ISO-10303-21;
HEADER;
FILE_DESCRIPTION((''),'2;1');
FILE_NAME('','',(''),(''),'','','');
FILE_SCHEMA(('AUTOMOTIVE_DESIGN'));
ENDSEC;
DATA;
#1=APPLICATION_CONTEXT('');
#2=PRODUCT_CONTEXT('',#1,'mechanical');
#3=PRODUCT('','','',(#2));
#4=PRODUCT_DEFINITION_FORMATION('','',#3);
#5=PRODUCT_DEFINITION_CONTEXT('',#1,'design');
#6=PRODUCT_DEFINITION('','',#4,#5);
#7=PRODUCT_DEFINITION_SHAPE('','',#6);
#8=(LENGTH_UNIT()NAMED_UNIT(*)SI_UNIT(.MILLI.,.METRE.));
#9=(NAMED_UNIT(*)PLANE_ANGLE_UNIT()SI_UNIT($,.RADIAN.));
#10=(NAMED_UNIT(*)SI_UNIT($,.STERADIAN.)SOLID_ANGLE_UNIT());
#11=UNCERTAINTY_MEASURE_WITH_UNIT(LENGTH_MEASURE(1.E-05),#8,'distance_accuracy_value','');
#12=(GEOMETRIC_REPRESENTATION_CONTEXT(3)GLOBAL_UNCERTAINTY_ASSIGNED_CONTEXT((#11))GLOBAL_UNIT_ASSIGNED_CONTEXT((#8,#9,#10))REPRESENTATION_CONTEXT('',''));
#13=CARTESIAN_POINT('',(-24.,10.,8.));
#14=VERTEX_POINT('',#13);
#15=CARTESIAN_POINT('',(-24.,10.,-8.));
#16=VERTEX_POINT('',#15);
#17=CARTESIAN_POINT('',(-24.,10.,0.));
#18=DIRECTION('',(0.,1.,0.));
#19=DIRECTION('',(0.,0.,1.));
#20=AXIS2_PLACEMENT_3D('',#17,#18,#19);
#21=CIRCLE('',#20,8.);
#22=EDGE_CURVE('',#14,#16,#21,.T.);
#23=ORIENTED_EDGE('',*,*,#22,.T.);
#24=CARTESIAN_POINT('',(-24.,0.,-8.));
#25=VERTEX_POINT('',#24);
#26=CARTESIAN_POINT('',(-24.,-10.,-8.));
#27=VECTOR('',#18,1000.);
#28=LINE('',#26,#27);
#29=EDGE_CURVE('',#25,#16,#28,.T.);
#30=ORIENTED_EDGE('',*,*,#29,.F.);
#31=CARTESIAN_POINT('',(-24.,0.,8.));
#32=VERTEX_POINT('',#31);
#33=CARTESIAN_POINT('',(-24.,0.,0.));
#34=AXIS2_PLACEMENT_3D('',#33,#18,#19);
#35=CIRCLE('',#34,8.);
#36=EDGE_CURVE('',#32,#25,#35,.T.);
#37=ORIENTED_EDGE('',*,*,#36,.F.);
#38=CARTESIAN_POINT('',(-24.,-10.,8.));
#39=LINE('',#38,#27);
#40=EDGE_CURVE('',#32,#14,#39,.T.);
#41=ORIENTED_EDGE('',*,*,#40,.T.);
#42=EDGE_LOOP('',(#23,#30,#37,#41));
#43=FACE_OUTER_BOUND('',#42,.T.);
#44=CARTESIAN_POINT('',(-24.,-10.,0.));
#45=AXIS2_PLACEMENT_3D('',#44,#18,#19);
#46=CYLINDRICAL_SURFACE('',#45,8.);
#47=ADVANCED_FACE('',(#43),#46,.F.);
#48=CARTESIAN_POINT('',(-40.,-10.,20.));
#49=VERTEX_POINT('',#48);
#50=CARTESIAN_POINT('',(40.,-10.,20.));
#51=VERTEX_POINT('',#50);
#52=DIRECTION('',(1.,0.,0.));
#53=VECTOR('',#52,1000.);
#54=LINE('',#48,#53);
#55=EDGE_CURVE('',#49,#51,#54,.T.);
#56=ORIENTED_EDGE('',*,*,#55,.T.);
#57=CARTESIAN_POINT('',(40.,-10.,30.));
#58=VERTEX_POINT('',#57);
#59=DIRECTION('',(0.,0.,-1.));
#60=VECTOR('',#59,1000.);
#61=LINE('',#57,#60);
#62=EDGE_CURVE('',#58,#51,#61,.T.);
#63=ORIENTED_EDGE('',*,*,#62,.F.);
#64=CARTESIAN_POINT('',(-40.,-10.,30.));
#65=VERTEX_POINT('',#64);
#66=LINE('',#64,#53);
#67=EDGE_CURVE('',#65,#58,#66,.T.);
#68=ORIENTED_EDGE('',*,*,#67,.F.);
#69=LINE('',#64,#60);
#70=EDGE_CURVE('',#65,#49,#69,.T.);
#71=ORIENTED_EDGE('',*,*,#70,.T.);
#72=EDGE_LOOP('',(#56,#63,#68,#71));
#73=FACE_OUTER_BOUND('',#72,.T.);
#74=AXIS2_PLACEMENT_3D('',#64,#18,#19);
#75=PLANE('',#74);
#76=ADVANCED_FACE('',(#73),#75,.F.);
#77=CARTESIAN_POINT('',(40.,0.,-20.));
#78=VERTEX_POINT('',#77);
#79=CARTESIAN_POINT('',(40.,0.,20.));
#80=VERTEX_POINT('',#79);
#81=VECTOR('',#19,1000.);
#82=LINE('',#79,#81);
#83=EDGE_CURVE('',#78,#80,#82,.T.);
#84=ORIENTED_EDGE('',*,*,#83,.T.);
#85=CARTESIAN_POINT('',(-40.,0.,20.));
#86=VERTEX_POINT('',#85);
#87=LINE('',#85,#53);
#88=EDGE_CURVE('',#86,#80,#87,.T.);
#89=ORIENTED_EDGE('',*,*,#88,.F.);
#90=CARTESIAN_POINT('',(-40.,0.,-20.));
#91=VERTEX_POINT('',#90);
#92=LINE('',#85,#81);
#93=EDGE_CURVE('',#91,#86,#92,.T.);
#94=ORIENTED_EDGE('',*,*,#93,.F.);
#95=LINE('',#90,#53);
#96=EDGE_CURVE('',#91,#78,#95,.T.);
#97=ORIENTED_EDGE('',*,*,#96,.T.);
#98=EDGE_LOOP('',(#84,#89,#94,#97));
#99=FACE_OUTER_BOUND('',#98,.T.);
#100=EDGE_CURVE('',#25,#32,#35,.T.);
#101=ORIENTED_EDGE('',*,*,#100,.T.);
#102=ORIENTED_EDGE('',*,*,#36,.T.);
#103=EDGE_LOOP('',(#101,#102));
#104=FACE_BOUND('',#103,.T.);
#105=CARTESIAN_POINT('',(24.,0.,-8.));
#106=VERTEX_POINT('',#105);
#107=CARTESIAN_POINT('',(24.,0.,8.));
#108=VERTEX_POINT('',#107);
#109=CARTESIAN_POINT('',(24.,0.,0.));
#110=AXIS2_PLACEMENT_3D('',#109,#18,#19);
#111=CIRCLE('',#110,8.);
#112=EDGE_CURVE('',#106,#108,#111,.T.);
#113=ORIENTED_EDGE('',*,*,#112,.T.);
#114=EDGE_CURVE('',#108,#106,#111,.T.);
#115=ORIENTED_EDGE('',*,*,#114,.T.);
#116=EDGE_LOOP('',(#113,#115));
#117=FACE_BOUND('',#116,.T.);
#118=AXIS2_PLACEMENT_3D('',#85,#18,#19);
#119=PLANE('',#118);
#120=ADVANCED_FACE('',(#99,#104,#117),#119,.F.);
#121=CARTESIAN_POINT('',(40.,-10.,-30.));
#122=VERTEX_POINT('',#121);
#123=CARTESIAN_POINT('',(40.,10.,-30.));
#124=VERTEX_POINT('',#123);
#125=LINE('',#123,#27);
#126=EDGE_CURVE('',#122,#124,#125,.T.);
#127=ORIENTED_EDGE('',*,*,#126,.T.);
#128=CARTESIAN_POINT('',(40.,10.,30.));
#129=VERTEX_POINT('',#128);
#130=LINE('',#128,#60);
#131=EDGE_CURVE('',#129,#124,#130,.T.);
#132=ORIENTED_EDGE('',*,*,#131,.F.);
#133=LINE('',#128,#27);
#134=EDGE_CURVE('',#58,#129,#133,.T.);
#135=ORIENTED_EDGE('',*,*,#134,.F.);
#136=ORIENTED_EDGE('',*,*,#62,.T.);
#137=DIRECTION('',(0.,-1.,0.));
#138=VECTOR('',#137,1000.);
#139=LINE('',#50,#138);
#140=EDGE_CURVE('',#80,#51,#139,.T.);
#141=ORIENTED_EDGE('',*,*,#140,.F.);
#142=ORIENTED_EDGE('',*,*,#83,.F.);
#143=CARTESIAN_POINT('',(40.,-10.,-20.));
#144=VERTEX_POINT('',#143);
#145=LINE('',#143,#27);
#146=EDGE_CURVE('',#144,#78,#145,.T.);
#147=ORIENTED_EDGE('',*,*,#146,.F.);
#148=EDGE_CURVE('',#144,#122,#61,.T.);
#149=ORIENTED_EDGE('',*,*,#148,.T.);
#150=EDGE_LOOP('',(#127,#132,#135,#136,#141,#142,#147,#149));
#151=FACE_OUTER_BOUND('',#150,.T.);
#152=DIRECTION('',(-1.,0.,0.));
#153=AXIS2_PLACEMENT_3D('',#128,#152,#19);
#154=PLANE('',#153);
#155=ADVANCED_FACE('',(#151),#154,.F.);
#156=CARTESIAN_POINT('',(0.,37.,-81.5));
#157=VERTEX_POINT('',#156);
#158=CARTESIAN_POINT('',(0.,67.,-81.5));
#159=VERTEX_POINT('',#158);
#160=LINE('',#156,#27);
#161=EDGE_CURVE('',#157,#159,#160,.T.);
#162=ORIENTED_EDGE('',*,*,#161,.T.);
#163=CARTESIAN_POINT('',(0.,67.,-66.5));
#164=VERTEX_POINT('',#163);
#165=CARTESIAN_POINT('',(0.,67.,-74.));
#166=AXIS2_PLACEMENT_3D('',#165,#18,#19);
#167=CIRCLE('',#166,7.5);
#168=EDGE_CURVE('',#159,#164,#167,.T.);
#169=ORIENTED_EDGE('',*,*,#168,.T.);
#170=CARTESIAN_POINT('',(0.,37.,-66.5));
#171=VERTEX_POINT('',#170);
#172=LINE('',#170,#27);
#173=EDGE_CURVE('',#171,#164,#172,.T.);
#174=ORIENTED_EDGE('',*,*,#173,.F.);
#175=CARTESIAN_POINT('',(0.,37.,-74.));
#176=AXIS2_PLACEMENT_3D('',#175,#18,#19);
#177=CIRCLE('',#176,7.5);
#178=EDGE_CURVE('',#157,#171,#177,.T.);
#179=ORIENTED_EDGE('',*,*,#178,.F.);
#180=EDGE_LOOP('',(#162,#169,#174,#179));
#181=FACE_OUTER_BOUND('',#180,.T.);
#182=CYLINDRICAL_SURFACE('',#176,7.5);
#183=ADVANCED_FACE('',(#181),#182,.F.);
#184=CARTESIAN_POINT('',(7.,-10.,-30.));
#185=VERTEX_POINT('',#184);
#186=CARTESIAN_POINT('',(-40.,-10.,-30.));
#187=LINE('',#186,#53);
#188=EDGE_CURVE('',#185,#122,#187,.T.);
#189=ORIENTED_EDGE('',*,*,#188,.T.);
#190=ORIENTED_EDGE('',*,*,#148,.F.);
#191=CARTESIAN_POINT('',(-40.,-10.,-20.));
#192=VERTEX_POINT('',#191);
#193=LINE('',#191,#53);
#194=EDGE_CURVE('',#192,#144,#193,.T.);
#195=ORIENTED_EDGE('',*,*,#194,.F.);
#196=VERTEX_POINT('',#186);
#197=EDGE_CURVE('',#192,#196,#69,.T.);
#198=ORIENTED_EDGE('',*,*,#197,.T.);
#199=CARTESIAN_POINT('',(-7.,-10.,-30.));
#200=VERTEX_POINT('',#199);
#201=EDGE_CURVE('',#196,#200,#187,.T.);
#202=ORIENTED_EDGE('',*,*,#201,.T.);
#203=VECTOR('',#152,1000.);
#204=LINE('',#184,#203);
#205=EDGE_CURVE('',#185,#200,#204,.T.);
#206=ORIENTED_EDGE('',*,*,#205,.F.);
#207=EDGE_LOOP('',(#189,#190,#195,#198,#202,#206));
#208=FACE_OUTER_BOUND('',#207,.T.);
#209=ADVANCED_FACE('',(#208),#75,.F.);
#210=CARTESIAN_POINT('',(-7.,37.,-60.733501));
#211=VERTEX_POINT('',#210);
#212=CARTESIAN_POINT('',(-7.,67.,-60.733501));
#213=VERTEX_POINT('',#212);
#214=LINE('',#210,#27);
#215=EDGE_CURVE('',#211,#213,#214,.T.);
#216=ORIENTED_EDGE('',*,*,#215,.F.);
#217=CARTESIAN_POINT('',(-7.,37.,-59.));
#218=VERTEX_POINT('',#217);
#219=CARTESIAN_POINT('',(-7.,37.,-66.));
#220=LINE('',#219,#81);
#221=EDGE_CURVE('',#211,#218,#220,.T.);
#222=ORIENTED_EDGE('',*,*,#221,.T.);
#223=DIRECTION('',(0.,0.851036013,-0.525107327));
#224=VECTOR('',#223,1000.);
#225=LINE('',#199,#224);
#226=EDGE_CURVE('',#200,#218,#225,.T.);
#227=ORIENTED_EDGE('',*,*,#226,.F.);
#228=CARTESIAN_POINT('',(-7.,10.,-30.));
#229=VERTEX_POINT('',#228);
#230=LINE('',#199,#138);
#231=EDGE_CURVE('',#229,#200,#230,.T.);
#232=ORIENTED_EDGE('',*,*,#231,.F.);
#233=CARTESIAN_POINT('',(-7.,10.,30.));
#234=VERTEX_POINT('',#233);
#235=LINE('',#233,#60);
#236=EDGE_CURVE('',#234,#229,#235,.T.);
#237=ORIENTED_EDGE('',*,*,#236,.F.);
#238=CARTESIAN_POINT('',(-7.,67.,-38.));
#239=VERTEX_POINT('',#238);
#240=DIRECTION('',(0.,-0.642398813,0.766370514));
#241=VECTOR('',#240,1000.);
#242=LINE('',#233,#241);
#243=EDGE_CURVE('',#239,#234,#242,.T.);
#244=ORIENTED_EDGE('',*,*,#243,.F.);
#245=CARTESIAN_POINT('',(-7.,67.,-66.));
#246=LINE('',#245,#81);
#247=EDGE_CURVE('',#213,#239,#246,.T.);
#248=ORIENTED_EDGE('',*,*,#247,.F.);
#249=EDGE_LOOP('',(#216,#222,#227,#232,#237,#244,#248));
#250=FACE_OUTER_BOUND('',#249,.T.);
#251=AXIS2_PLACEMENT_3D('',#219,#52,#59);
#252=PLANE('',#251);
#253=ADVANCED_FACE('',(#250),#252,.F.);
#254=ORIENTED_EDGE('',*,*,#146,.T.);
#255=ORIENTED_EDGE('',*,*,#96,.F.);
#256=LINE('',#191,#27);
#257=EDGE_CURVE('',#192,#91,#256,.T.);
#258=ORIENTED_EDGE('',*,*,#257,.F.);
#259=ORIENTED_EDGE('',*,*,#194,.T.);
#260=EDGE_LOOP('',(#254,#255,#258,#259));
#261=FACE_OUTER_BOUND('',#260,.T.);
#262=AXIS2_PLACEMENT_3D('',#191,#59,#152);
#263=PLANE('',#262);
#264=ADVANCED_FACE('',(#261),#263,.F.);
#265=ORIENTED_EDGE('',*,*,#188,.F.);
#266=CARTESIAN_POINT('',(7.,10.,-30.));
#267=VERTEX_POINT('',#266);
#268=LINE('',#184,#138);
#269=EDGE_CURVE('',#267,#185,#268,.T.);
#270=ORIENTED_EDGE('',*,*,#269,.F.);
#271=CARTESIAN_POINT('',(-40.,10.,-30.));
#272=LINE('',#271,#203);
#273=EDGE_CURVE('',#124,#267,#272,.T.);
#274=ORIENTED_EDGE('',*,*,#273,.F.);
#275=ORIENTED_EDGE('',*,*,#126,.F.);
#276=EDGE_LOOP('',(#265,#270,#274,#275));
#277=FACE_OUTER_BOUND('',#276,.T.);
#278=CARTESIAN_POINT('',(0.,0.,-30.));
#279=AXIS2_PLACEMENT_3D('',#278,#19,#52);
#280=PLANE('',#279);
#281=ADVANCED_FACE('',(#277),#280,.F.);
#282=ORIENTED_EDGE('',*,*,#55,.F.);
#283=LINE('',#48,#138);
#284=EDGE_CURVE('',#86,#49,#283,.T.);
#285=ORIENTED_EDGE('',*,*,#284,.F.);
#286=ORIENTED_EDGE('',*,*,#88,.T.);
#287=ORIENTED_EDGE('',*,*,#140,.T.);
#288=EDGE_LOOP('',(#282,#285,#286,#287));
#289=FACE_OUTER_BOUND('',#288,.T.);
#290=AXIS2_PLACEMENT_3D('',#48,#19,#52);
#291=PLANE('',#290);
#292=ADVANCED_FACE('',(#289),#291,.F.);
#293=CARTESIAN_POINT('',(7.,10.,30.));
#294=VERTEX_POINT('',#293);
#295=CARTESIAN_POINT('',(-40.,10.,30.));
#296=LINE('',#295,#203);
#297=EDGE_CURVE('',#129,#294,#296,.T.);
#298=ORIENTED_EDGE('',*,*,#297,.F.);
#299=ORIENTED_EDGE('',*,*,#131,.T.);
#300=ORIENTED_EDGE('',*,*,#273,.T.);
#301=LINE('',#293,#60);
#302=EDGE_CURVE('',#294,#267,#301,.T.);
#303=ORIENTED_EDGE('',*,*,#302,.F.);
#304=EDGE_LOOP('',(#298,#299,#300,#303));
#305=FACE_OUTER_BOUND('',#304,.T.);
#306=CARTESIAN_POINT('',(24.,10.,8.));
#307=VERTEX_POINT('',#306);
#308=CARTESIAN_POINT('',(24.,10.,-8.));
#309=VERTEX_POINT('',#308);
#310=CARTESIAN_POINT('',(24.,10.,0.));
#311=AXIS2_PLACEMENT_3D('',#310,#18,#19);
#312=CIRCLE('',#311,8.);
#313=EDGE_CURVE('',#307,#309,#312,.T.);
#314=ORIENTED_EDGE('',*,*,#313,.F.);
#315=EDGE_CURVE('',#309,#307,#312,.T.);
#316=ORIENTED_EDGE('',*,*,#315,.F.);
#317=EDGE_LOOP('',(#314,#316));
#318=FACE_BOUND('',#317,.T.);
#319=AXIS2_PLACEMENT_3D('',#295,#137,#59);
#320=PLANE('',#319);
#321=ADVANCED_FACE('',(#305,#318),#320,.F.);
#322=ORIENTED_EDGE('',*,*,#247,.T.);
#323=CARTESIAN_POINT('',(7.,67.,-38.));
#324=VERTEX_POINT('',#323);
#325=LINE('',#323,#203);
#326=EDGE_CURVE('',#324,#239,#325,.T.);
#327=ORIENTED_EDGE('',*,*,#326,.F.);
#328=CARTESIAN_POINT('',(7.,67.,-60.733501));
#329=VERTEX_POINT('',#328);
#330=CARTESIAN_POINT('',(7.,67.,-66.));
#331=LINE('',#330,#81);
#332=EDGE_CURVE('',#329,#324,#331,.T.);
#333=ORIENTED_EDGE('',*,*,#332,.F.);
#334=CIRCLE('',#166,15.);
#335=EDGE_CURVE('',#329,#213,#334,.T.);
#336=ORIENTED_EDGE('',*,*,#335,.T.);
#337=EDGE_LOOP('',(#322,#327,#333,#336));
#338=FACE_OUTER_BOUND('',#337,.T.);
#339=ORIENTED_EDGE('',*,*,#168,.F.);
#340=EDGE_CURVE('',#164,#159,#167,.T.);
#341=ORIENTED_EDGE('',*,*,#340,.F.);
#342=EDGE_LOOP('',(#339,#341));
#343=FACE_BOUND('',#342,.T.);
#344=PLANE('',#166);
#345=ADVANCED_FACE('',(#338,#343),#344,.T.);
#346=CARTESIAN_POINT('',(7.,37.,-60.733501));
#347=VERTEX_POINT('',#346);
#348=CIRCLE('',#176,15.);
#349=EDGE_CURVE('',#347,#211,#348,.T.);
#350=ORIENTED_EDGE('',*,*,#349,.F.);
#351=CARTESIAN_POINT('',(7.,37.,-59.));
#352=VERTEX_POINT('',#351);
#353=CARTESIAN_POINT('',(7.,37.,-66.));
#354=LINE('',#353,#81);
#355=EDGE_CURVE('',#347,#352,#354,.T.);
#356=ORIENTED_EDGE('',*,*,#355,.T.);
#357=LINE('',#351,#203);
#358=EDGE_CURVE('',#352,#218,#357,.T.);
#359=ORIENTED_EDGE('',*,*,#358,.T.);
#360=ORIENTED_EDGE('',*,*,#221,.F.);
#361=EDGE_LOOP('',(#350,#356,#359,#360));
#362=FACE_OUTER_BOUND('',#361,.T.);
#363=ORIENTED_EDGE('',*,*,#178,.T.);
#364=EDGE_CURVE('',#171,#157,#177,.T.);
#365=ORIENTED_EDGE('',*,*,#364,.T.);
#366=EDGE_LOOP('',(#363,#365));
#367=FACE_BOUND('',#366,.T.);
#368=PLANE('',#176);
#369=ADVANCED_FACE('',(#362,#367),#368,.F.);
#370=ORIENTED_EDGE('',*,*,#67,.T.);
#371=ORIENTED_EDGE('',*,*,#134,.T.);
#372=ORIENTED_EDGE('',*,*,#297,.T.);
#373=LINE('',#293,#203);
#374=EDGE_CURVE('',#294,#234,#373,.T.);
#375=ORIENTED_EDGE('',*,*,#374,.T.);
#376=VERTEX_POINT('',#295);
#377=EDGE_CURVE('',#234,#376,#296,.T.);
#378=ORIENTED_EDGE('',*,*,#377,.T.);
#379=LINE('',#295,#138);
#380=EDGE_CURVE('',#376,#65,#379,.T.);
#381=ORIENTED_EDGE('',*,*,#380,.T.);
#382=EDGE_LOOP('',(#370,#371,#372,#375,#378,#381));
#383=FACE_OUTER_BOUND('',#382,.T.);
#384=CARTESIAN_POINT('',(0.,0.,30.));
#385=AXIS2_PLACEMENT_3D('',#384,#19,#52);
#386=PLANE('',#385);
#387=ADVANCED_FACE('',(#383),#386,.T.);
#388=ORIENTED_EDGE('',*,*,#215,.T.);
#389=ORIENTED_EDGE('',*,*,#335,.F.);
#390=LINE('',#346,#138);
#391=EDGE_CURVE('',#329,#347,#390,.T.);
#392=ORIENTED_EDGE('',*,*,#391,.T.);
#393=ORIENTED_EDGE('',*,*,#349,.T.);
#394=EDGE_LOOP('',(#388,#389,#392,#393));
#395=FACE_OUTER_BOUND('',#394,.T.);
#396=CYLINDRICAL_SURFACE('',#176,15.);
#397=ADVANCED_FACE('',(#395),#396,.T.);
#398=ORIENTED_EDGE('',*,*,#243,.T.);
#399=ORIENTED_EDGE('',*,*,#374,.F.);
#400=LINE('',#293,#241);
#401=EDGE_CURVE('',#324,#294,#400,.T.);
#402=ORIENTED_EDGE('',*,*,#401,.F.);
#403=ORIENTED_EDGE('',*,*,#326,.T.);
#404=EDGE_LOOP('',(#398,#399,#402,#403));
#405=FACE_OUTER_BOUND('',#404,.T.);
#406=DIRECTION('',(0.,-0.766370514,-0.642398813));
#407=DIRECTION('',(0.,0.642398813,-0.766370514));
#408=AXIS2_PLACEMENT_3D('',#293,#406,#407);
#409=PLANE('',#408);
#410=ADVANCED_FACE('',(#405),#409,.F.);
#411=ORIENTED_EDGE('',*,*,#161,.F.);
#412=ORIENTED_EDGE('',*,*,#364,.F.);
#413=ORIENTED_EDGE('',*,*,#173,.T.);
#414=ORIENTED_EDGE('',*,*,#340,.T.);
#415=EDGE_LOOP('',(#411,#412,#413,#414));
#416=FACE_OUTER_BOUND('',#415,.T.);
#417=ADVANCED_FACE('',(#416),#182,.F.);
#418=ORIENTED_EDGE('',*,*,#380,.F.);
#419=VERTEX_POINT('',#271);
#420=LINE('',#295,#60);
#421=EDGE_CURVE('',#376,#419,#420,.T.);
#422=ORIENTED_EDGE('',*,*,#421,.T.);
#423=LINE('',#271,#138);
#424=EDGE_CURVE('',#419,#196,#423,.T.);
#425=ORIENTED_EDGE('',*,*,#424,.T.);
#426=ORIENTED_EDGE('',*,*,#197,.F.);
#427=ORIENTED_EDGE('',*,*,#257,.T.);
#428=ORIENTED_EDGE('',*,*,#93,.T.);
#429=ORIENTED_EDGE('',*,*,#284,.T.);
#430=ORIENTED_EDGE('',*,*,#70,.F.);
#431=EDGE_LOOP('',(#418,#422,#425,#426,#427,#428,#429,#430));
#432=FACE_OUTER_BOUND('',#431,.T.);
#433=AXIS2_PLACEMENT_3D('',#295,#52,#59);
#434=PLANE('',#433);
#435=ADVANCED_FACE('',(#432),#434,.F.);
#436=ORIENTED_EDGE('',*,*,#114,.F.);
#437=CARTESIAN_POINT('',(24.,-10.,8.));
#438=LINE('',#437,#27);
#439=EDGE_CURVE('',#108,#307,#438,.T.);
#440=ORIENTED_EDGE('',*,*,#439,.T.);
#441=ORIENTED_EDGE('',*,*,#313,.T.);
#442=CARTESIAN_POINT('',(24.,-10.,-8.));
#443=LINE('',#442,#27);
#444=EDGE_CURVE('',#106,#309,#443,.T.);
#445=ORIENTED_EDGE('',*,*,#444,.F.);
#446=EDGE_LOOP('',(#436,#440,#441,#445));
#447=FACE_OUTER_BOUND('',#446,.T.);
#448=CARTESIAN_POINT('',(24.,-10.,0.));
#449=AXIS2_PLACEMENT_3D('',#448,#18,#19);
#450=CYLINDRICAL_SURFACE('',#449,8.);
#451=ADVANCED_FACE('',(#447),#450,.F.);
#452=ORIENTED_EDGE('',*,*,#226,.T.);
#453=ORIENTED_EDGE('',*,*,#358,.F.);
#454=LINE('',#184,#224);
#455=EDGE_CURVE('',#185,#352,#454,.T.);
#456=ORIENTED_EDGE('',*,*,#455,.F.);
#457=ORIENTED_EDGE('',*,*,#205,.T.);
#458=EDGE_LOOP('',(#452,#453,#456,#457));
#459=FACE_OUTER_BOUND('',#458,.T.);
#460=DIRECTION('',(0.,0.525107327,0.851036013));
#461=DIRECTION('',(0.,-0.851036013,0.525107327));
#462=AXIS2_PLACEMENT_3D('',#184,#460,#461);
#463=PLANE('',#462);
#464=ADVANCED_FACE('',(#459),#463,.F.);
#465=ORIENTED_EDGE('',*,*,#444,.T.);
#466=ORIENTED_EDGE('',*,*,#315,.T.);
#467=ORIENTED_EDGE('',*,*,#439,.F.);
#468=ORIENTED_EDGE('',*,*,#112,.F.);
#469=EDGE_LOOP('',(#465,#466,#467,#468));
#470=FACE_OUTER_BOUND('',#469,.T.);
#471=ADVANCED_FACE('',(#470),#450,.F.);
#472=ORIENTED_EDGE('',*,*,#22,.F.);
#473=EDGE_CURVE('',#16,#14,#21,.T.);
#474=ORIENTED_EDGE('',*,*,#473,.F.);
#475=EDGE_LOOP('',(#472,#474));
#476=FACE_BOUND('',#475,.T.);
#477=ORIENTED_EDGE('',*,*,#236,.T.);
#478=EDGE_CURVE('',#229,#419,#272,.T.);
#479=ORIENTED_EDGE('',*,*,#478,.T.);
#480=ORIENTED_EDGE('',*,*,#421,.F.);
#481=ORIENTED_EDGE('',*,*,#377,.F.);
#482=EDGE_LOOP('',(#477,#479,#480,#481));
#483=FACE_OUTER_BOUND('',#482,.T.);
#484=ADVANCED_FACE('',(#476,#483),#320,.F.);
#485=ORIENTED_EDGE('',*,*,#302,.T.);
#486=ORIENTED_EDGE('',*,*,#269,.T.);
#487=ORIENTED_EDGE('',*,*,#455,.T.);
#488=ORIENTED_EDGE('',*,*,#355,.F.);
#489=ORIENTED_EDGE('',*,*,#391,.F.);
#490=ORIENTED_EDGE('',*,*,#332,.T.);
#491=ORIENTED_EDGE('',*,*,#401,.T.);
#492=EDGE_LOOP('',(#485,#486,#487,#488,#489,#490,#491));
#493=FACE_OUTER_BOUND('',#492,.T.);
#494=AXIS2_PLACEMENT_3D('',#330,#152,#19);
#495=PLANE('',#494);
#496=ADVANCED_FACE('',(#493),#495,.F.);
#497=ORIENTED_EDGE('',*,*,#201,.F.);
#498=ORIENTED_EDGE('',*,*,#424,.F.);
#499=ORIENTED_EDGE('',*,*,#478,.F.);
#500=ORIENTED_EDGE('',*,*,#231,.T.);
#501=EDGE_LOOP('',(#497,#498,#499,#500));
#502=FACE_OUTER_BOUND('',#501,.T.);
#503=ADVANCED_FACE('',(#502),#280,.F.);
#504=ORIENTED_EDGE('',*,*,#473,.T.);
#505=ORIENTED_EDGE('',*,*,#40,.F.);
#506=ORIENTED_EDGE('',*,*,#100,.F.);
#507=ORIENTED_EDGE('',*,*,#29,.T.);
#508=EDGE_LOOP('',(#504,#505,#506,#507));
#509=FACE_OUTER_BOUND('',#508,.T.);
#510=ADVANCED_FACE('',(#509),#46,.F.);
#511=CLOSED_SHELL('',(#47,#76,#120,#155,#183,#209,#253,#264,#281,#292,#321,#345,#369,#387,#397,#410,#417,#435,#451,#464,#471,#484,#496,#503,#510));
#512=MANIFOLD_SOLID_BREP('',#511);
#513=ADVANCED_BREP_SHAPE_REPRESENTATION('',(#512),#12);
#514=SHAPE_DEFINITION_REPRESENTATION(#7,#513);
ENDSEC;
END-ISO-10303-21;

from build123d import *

# Parameters (mm, degrees)
BASE_PROFILE_SKETCH_W = 80
BASE_PROFILE_SKETCH_H = 20
BASE_BLOCK_DEPTH      = 30
ROUND_START           = 57
ROUND_BOSS_SKETCH_R   = 15
ROUND_BOSS_SKETCH_R_2 = 7.5
ROUND_BOSS_DEPTH      = 30
INCLINED_ARM_DEPTH    = 7
ARM_WEB_SKETCH_W      = 14
ARM_WEB_SKETCH_H      = 30
ARM_WEB_DEPTH         = 7
BASE_SLOT_SKETCH_W    = 40
BASE_SLOT_SKETCH_H    = 10
BASE_SLOT_40X10_DEPTH = 138.149553408
HOLE_CUT_SKETCH_R     = 8
HOLES_16_DEPTH        = 114.004424692


with BuildPart() as part:
    # Base Profile Sketch → Base Block (new, symmetric)
    with BuildSketch(Plane.XY):
        Rectangle(BASE_PROFILE_SKETCH_W, BASE_PROFILE_SKETCH_H)
    extrude(amount=BASE_BLOCK_DEPTH, both=True)

    # Inclined Arm Sketch → Inclined Arm (add, symmetric)
    with BuildSketch(Plane(origin=(0, 0, 0), x_dir=(0, 0, -1), z_dir=(1, 0, 0))):
        Polygon((-30, 10), (38, 67), (59, 67), (59, 37), (30, -10), (30, 10), align=None)
    extrude(amount=INCLINED_ARM_DEPTH, both=True)



with BuildPart() as body_2:
    # Round Boss Sketch → Round Boss (new body)
    with BuildSketch(Plane(origin=(0, 10, 0), x_dir=(1, 0, 0), z_dir=(0, 1, 0)).offset(ROUND_START)):
        with Locations(Location((0, 74, 0), (0, 0, 270))):
            Circle(ROUND_BOSS_SKETCH_R)
        with Locations(Location((0, 74, 0), (0, 0, 270))):
            Circle(ROUND_BOSS_SKETCH_R_2, mode=Mode.SUBTRACT)
    extrude(amount=-ROUND_BOSS_DEPTH)


with BuildPart() as part_1:
    add(part.part)

    add(body_2.part)  # Arm Web merges body 2
    # Arm Web Sketch → Arm Web (add, symmetric)
    with BuildSketch(Plane(origin=(0, 0, -59), x_dir=(-1, 0, 0), z_dir=(0, 0, -1))):
        with Locations((0, 52)):
            Rectangle(ARM_WEB_SKETCH_W, ARM_WEB_SKETCH_H)
    extrude(amount=ARM_WEB_DEPTH, both=True)

    # Base Slot Sketch → Base Slot 40x10 (cut, through all)
    with BuildSketch(Plane(origin=(40, 0, 0), x_dir=(0, 0, -1), z_dir=(1, 0, 0))):
        with Locations((0, -5)):
            Rectangle(BASE_SLOT_SKETCH_W, BASE_SLOT_SKETCH_H)
    extrude(amount=-BASE_SLOT_40X10_DEPTH, mode=Mode.SUBTRACT)

    # Hole Cut Sketch → Holes Ø16 (cut, through all)
    with BuildSketch(Plane(origin=(0, 10, 0), x_dir=(1, 0, 0), z_dir=(0, 1, 0))):
        with Locations(Location((-24, 0, 0), (0, 0, 270))):
            Circle(HOLE_CUT_SKETCH_R)
        with Locations(Location((24, 0, 0), (0, 0, 270))):
            Circle(HOLE_CUT_SKETCH_R)
    extrude(amount=-HOLES_16_DEPTH, mode=Mode.SUBTRACT)


solid = part_1.part
